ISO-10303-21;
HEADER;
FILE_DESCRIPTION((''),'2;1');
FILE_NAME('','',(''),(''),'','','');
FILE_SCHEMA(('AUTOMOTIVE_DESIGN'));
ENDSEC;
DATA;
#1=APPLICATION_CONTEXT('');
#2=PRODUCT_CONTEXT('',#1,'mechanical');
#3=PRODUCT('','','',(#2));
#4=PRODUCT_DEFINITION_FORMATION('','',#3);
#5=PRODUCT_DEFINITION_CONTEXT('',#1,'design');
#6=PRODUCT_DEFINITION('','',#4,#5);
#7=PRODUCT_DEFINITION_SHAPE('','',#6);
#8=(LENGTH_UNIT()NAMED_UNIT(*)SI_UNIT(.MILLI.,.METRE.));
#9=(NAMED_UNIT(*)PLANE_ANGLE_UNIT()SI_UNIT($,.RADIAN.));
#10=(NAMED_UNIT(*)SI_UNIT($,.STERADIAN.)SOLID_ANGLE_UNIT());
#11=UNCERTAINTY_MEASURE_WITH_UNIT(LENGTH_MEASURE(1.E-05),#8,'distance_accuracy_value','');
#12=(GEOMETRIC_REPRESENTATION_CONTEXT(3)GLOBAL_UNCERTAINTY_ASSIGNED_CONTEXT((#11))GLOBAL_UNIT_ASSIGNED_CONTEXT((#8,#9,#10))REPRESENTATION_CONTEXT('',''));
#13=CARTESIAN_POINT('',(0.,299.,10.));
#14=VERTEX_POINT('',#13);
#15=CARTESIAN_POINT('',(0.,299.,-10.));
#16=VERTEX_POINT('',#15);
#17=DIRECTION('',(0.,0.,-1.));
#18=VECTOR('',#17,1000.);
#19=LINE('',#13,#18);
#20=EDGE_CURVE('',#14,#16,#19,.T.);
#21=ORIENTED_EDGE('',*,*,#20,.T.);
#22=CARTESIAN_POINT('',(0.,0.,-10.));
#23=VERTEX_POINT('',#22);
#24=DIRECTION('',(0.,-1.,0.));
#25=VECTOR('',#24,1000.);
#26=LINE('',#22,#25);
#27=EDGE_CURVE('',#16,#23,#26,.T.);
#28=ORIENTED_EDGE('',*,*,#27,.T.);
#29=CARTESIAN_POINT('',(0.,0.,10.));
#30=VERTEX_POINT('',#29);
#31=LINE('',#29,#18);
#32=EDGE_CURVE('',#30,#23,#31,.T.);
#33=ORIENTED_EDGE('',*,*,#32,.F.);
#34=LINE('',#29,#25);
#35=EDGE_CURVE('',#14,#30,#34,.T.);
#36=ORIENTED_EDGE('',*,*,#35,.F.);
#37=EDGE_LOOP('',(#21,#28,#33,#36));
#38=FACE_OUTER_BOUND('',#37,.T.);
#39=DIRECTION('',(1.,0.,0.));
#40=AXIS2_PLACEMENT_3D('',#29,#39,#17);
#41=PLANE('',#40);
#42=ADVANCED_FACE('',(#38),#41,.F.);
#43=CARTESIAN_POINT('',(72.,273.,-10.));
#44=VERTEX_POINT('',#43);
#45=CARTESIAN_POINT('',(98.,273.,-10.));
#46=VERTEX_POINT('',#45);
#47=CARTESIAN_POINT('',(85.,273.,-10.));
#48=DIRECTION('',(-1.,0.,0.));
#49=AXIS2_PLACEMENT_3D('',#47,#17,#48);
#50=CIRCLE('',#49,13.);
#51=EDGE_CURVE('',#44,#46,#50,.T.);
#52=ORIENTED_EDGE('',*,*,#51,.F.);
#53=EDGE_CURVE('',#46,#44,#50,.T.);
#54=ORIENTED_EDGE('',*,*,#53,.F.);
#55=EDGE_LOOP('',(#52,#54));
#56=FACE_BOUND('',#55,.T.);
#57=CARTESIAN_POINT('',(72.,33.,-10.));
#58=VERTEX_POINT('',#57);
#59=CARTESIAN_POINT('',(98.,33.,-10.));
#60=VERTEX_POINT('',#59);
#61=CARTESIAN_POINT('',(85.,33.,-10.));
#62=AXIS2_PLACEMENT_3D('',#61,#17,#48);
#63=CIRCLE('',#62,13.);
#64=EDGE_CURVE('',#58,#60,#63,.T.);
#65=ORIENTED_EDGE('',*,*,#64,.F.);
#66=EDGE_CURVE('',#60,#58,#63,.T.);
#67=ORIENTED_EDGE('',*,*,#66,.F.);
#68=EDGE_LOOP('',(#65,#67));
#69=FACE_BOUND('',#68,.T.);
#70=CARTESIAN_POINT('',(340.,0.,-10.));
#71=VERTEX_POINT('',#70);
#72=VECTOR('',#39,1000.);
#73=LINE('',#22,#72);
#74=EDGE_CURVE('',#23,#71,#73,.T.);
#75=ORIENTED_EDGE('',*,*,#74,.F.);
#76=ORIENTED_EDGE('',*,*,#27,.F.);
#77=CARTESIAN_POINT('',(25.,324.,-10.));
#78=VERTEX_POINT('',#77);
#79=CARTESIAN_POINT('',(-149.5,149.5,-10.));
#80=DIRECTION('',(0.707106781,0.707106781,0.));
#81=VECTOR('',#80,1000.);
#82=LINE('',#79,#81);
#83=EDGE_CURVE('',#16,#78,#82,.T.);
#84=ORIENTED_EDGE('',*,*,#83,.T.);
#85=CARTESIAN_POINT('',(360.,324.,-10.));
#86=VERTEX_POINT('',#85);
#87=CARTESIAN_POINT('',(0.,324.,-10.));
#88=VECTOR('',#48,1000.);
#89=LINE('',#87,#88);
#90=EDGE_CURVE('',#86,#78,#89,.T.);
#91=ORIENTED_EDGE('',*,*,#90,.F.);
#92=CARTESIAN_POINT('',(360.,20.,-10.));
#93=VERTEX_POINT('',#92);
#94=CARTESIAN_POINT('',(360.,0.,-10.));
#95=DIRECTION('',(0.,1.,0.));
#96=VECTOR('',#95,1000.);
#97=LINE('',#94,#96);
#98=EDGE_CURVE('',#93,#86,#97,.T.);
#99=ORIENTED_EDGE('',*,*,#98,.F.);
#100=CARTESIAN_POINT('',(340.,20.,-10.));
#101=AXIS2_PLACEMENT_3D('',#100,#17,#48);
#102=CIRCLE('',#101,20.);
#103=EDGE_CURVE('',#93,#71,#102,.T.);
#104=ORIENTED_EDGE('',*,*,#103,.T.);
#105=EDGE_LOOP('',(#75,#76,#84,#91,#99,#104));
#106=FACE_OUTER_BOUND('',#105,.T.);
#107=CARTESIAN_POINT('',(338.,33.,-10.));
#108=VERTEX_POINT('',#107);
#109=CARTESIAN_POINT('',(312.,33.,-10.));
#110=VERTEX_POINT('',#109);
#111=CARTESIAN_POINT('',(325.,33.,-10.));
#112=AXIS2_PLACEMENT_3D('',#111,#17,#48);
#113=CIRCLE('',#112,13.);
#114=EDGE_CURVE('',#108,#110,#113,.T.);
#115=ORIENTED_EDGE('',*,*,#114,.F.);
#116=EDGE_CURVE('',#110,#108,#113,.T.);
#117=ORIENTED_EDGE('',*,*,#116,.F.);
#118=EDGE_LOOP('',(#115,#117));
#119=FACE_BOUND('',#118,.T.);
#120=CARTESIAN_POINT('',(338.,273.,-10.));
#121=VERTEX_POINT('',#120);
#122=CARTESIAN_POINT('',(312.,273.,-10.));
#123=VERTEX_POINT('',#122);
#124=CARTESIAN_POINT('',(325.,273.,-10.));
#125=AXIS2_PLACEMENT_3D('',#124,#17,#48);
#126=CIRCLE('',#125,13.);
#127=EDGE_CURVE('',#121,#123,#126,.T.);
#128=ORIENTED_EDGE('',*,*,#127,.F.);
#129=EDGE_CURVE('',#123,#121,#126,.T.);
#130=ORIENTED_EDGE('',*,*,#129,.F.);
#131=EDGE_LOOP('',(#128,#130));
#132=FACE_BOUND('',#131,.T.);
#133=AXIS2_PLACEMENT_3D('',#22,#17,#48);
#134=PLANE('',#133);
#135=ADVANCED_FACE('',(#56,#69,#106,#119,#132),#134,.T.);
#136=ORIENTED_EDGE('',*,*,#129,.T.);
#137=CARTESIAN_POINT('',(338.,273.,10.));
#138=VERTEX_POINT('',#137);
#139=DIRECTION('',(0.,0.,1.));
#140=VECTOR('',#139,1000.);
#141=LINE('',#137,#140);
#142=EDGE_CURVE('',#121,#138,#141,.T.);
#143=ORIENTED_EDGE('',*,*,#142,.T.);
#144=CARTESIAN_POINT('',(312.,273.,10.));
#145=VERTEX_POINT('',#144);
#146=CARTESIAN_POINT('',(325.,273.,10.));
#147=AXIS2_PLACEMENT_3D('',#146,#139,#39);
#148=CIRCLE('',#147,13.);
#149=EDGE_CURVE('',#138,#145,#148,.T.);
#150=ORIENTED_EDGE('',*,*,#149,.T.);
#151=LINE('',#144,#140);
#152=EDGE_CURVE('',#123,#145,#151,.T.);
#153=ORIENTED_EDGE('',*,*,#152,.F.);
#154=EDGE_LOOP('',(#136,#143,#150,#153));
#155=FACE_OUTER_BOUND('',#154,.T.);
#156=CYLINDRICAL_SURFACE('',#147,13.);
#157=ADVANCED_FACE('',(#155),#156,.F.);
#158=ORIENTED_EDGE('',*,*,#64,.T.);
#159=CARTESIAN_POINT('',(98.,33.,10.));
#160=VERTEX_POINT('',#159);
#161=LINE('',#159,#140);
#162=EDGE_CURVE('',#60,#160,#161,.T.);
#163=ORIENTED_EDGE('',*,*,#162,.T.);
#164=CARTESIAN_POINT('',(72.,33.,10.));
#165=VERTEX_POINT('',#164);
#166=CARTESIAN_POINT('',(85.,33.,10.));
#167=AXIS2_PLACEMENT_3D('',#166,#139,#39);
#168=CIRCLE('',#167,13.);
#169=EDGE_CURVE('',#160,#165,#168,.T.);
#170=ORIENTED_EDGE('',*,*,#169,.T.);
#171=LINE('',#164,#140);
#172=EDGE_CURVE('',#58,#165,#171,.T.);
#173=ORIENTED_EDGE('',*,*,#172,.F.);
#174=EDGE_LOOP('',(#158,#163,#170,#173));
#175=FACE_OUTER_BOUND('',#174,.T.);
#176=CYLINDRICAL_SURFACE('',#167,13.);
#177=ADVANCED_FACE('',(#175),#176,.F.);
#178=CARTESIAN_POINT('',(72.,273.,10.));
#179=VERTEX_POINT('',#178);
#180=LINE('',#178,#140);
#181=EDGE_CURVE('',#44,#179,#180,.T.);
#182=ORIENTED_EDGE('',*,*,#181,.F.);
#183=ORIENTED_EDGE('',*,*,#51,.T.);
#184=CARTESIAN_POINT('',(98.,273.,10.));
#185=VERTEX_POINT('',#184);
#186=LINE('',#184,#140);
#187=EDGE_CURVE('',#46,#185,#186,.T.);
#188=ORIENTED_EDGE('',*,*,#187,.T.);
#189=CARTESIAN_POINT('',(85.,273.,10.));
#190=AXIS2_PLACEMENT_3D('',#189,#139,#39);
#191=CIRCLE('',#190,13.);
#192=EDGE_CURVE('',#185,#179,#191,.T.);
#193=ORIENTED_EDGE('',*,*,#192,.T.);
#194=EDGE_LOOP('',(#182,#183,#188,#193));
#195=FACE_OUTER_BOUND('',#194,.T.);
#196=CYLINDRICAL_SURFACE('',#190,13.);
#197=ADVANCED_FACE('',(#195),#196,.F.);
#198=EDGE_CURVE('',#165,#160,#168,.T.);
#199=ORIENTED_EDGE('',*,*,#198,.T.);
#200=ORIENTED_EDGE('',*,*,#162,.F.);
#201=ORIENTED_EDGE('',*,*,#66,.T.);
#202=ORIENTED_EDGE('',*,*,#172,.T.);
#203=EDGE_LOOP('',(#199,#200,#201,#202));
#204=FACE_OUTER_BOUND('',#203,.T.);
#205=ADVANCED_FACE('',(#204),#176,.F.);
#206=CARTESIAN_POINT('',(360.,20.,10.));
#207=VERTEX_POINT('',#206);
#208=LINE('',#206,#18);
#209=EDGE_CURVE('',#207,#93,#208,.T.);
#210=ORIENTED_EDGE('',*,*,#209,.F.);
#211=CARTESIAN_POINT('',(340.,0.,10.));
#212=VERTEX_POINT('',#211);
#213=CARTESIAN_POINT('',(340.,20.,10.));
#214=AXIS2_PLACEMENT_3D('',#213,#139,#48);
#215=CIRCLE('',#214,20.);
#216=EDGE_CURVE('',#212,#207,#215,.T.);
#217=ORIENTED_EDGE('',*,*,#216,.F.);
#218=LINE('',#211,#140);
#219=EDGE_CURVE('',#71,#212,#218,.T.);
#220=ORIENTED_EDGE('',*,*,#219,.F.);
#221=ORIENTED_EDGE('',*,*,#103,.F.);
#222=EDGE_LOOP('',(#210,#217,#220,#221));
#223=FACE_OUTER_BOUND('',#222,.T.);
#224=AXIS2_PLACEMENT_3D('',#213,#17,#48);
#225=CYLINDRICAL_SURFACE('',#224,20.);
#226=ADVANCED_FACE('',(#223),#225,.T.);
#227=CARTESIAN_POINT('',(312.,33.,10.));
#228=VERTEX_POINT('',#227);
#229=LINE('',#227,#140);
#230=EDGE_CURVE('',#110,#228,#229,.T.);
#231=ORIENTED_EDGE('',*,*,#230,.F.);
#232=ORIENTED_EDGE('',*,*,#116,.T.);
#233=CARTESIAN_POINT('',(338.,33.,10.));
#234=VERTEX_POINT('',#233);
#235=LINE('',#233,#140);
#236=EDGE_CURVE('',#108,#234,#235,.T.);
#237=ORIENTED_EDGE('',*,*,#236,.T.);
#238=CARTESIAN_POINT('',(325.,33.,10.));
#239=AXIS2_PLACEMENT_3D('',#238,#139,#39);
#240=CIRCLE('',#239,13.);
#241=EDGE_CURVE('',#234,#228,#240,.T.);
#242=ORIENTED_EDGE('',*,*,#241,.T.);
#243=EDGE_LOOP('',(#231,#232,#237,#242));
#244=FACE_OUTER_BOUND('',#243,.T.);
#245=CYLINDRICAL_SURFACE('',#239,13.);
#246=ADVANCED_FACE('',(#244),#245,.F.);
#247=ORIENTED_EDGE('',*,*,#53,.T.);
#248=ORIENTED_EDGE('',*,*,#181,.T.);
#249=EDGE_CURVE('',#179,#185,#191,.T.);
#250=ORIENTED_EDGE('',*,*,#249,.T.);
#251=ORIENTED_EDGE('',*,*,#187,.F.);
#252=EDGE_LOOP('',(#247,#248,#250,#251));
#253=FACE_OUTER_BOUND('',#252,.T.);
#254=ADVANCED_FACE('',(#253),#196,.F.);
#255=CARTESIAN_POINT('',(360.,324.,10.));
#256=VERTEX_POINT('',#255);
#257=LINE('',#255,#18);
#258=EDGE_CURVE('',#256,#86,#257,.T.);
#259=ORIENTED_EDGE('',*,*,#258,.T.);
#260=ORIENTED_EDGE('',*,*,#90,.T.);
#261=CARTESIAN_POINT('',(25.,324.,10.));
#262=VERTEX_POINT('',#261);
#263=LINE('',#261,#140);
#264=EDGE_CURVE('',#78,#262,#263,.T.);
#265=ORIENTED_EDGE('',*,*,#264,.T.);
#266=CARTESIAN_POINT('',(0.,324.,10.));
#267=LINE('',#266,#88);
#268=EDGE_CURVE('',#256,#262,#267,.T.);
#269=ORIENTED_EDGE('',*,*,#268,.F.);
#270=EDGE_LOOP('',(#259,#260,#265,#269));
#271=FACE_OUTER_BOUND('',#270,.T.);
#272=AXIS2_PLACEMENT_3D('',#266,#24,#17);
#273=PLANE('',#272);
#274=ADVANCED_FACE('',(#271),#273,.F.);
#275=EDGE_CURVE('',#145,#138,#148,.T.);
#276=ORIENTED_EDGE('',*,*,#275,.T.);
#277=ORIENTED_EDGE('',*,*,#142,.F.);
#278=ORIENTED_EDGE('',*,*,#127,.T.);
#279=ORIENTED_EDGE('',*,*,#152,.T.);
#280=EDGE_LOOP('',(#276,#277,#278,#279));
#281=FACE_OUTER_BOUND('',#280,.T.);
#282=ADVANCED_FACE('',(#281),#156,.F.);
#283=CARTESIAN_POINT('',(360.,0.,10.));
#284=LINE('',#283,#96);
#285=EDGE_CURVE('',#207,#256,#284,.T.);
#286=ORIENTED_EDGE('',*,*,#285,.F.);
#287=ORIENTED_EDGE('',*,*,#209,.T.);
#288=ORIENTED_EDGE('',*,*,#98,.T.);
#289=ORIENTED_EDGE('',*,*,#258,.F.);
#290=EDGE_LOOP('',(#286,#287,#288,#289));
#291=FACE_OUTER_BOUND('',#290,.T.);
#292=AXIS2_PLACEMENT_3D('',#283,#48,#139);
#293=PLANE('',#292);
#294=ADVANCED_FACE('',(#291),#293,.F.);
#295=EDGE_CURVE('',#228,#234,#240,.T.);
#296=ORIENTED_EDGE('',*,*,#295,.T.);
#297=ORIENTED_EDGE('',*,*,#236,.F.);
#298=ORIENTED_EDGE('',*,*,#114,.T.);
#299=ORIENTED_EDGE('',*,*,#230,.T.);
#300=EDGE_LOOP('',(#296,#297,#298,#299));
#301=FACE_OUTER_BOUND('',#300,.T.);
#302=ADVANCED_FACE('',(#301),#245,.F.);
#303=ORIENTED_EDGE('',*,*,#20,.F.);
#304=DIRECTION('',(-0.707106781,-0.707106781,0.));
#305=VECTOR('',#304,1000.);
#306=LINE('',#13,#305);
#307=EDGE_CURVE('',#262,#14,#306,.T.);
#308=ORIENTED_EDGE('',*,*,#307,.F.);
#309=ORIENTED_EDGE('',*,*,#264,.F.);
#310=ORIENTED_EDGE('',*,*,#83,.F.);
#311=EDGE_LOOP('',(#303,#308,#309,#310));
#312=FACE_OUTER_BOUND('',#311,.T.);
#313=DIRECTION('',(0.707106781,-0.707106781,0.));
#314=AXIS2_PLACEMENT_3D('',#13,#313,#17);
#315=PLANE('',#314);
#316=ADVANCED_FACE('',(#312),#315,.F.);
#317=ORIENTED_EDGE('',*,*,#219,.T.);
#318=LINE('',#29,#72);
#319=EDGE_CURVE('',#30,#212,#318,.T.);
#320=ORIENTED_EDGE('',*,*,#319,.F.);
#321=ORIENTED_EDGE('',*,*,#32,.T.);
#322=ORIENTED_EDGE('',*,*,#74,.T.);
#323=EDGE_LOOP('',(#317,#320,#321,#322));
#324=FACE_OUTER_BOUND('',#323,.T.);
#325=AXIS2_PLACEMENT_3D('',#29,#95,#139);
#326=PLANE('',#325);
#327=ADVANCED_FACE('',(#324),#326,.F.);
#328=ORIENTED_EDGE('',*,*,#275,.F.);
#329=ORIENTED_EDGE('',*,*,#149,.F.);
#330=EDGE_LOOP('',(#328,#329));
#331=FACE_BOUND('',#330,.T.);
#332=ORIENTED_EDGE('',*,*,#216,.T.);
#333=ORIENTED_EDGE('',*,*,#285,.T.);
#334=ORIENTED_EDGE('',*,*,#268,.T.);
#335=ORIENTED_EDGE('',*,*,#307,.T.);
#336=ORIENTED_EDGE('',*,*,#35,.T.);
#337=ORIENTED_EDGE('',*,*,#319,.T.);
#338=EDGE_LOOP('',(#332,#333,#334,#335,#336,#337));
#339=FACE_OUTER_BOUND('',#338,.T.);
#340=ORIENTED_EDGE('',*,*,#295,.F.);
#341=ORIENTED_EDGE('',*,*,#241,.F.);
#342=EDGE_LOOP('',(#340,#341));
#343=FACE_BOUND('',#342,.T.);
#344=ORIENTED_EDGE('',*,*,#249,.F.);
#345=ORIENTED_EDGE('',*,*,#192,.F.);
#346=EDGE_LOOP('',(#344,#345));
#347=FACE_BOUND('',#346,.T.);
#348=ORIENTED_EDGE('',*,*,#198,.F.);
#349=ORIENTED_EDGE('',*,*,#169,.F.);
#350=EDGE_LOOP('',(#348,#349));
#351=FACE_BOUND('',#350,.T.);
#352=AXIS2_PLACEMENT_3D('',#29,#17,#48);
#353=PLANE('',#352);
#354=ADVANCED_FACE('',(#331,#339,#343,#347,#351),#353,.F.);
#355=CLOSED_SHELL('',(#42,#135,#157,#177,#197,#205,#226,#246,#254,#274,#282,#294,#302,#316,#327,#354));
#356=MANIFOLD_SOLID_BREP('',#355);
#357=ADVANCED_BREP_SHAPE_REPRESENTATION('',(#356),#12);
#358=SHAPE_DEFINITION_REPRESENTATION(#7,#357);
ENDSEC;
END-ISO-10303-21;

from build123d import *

# Parameters (mm, degrees)
SKETCH1_W                  = 360
SKETCH1_H                  = 324
BOSS_EXTRUDE1_DEPTH        = 10
CHAMFER1_SIZE              = 25
FILLET1_R                  = 20
F_25_0_25_DIAMETER_HOLE1_D = 26


with BuildPart() as part:
    # Sketch1 → Boss-Extrude1 (new, symmetric)
    with BuildSketch(Plane.XY):
        with Locations((180, 162)):
            Rectangle(SKETCH1_W, SKETCH1_H)
    extrude(amount=BOSS_EXTRUDE1_DEPTH, both=True)

    # Chamfer1
    chamfer1_edges = [part.edges().sort_by_distance(p)[0] for p in [
        (0, 324, 0),
    ]]
    chamfer(chamfer1_edges, length=CHAMFER1_SIZE)

    # Fillet1
    fillet1_edges = [part.edges().sort_by_distance(p)[0] for p in [
        (360, 0, 0),
    ]]
    fillet(fillet1_edges, radius=FILLET1_R)

    # Ø25.0 (25) Diameter Hole1 (through all)
    with Locations(Plane.XY.offset(10)):
        with Locations((85, 33), (325, 33), (325, 273), (85, 273)):
            Hole(F_25_0_25_DIAMETER_HOLE1_D / 2)


solid = part.part
